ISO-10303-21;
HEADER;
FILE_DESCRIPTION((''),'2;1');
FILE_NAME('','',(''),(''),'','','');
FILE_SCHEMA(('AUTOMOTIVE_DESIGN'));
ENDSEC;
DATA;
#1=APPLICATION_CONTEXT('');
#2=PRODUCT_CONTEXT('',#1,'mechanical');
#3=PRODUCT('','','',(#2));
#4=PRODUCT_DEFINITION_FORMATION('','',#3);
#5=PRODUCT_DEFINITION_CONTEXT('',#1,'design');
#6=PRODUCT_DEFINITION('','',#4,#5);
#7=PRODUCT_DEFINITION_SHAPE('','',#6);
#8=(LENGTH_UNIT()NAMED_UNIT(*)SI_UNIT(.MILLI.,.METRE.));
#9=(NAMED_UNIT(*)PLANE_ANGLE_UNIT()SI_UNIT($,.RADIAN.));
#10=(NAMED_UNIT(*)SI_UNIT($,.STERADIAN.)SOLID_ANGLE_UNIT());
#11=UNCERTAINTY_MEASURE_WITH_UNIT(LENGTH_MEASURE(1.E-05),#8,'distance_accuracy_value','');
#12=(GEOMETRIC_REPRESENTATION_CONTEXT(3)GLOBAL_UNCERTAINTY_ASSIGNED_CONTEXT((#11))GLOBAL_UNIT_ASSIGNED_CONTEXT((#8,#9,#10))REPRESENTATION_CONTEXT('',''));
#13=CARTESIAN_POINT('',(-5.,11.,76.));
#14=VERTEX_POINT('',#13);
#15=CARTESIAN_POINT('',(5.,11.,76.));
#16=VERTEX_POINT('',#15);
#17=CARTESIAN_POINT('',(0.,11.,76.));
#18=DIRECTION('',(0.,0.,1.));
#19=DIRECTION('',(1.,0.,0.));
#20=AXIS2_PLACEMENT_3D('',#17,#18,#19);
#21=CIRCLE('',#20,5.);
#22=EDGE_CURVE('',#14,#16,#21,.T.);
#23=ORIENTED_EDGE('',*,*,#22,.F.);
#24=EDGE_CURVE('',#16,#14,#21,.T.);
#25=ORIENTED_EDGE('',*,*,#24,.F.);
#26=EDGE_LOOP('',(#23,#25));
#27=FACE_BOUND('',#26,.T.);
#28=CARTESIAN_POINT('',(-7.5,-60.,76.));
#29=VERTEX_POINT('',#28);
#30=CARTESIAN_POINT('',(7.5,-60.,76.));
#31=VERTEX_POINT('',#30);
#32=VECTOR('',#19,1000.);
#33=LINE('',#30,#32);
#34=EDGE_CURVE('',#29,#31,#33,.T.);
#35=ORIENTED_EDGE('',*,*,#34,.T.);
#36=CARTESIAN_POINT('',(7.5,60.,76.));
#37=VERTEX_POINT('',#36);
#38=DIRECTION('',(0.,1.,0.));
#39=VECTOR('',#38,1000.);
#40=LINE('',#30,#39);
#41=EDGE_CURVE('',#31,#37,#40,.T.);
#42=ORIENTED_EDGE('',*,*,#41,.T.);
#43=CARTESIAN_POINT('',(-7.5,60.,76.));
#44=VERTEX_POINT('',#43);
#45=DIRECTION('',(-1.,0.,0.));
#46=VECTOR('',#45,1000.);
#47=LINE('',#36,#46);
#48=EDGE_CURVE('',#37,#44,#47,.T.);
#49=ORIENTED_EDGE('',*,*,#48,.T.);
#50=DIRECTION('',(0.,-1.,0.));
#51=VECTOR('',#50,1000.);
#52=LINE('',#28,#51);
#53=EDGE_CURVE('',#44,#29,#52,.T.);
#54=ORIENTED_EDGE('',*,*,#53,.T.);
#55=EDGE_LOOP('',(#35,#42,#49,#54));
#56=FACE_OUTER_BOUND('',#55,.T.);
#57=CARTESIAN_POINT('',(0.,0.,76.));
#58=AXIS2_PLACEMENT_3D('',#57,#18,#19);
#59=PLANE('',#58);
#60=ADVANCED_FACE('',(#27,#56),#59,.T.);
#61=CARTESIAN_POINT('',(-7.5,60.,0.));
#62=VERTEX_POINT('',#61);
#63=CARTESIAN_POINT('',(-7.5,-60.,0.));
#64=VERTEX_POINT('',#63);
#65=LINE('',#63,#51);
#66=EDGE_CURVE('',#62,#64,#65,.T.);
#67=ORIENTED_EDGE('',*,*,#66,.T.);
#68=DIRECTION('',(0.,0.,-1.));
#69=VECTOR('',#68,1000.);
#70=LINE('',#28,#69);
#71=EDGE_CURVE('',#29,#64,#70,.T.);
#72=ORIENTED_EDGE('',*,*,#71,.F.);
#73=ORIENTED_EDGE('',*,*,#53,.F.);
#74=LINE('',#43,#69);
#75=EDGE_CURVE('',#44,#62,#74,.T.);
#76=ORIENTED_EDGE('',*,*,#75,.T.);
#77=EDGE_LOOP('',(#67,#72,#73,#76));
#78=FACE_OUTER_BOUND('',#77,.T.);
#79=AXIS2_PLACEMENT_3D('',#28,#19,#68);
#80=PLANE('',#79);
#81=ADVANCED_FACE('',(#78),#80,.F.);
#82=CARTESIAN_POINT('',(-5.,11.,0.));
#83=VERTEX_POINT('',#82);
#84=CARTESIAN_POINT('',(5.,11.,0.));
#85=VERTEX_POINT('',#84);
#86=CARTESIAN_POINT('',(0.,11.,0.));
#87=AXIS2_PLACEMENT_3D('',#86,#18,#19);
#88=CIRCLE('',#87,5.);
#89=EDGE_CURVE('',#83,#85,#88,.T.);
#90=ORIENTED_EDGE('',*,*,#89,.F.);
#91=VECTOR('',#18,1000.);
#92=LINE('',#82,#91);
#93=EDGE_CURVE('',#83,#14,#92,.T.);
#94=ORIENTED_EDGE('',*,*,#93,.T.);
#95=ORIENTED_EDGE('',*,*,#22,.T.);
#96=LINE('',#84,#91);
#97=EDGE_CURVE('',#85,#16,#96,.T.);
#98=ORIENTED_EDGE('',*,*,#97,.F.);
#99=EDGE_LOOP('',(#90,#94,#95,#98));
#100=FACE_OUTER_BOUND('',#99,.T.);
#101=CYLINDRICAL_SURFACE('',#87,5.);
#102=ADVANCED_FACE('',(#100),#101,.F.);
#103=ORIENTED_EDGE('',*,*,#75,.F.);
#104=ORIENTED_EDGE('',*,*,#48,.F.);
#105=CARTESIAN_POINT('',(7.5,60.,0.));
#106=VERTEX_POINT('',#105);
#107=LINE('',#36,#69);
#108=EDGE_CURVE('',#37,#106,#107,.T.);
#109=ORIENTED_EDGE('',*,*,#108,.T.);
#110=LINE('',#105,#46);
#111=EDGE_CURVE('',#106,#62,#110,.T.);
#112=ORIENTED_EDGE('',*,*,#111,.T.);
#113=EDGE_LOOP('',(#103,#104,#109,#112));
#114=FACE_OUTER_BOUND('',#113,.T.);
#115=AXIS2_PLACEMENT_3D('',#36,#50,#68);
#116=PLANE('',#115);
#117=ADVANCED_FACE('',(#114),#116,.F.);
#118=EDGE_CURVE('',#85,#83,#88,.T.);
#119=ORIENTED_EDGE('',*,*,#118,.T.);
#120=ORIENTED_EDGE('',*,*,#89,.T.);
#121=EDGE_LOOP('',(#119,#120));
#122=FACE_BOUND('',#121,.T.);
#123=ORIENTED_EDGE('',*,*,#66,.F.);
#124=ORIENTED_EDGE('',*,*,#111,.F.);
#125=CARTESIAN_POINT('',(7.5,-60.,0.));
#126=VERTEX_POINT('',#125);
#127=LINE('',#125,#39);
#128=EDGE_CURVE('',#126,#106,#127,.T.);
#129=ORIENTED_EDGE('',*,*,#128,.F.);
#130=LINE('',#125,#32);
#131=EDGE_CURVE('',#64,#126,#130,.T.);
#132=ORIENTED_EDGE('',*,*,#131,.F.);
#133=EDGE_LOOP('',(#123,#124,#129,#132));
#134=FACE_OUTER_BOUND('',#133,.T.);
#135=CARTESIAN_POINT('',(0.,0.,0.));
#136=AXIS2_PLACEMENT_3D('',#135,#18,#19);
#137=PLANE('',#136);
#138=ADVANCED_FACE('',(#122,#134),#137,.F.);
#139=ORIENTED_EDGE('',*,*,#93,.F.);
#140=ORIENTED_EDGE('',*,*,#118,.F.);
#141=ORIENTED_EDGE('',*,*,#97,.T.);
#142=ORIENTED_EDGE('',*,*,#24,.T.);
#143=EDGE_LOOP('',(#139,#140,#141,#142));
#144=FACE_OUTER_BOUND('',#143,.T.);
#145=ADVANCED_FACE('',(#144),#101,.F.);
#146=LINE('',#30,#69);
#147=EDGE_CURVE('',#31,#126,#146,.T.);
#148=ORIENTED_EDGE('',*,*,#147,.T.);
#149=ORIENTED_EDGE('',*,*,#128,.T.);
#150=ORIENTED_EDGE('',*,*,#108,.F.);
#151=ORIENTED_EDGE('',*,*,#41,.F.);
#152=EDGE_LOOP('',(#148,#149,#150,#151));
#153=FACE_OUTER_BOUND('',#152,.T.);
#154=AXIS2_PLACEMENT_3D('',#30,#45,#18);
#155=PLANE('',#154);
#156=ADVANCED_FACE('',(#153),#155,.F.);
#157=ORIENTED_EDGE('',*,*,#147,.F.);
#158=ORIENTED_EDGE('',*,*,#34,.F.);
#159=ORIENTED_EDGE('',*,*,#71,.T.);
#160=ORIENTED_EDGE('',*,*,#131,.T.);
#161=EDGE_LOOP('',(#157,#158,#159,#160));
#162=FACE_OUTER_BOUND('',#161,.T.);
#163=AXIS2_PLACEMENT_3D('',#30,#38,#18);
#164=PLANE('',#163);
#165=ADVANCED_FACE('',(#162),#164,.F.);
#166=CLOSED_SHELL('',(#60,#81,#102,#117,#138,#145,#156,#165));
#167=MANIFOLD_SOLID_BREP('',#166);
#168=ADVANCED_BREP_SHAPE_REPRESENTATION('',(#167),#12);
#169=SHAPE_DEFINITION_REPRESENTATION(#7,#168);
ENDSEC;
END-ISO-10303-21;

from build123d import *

# Parameters (mm, degrees)
SKETCH1_W           = 15
SKETCH1_H           = 120
BOSS_EXTRUDE1_DEPTH = 76
SKETCH2_R           = 5
CUT_EXTRUDE2_DEPTH  = 98.119771417


with BuildPart() as part:
    # Sketch1 → Boss-Extrude1 (new body)
    with BuildSketch(Plane.XY):
        Rectangle(SKETCH1_W, SKETCH1_H)
    extrude(amount=BOSS_EXTRUDE1_DEPTH)

    # Sketch2 → Cut-Extrude2 (cut, through all)
    with BuildSketch(Plane.XY.offset(76)):
        with Locations((0, 11)):
            Circle(SKETCH2_R)
    extrude(amount=-CUT_EXTRUDE2_DEPTH, mode=Mode.SUBTRACT)


solid = part.part
